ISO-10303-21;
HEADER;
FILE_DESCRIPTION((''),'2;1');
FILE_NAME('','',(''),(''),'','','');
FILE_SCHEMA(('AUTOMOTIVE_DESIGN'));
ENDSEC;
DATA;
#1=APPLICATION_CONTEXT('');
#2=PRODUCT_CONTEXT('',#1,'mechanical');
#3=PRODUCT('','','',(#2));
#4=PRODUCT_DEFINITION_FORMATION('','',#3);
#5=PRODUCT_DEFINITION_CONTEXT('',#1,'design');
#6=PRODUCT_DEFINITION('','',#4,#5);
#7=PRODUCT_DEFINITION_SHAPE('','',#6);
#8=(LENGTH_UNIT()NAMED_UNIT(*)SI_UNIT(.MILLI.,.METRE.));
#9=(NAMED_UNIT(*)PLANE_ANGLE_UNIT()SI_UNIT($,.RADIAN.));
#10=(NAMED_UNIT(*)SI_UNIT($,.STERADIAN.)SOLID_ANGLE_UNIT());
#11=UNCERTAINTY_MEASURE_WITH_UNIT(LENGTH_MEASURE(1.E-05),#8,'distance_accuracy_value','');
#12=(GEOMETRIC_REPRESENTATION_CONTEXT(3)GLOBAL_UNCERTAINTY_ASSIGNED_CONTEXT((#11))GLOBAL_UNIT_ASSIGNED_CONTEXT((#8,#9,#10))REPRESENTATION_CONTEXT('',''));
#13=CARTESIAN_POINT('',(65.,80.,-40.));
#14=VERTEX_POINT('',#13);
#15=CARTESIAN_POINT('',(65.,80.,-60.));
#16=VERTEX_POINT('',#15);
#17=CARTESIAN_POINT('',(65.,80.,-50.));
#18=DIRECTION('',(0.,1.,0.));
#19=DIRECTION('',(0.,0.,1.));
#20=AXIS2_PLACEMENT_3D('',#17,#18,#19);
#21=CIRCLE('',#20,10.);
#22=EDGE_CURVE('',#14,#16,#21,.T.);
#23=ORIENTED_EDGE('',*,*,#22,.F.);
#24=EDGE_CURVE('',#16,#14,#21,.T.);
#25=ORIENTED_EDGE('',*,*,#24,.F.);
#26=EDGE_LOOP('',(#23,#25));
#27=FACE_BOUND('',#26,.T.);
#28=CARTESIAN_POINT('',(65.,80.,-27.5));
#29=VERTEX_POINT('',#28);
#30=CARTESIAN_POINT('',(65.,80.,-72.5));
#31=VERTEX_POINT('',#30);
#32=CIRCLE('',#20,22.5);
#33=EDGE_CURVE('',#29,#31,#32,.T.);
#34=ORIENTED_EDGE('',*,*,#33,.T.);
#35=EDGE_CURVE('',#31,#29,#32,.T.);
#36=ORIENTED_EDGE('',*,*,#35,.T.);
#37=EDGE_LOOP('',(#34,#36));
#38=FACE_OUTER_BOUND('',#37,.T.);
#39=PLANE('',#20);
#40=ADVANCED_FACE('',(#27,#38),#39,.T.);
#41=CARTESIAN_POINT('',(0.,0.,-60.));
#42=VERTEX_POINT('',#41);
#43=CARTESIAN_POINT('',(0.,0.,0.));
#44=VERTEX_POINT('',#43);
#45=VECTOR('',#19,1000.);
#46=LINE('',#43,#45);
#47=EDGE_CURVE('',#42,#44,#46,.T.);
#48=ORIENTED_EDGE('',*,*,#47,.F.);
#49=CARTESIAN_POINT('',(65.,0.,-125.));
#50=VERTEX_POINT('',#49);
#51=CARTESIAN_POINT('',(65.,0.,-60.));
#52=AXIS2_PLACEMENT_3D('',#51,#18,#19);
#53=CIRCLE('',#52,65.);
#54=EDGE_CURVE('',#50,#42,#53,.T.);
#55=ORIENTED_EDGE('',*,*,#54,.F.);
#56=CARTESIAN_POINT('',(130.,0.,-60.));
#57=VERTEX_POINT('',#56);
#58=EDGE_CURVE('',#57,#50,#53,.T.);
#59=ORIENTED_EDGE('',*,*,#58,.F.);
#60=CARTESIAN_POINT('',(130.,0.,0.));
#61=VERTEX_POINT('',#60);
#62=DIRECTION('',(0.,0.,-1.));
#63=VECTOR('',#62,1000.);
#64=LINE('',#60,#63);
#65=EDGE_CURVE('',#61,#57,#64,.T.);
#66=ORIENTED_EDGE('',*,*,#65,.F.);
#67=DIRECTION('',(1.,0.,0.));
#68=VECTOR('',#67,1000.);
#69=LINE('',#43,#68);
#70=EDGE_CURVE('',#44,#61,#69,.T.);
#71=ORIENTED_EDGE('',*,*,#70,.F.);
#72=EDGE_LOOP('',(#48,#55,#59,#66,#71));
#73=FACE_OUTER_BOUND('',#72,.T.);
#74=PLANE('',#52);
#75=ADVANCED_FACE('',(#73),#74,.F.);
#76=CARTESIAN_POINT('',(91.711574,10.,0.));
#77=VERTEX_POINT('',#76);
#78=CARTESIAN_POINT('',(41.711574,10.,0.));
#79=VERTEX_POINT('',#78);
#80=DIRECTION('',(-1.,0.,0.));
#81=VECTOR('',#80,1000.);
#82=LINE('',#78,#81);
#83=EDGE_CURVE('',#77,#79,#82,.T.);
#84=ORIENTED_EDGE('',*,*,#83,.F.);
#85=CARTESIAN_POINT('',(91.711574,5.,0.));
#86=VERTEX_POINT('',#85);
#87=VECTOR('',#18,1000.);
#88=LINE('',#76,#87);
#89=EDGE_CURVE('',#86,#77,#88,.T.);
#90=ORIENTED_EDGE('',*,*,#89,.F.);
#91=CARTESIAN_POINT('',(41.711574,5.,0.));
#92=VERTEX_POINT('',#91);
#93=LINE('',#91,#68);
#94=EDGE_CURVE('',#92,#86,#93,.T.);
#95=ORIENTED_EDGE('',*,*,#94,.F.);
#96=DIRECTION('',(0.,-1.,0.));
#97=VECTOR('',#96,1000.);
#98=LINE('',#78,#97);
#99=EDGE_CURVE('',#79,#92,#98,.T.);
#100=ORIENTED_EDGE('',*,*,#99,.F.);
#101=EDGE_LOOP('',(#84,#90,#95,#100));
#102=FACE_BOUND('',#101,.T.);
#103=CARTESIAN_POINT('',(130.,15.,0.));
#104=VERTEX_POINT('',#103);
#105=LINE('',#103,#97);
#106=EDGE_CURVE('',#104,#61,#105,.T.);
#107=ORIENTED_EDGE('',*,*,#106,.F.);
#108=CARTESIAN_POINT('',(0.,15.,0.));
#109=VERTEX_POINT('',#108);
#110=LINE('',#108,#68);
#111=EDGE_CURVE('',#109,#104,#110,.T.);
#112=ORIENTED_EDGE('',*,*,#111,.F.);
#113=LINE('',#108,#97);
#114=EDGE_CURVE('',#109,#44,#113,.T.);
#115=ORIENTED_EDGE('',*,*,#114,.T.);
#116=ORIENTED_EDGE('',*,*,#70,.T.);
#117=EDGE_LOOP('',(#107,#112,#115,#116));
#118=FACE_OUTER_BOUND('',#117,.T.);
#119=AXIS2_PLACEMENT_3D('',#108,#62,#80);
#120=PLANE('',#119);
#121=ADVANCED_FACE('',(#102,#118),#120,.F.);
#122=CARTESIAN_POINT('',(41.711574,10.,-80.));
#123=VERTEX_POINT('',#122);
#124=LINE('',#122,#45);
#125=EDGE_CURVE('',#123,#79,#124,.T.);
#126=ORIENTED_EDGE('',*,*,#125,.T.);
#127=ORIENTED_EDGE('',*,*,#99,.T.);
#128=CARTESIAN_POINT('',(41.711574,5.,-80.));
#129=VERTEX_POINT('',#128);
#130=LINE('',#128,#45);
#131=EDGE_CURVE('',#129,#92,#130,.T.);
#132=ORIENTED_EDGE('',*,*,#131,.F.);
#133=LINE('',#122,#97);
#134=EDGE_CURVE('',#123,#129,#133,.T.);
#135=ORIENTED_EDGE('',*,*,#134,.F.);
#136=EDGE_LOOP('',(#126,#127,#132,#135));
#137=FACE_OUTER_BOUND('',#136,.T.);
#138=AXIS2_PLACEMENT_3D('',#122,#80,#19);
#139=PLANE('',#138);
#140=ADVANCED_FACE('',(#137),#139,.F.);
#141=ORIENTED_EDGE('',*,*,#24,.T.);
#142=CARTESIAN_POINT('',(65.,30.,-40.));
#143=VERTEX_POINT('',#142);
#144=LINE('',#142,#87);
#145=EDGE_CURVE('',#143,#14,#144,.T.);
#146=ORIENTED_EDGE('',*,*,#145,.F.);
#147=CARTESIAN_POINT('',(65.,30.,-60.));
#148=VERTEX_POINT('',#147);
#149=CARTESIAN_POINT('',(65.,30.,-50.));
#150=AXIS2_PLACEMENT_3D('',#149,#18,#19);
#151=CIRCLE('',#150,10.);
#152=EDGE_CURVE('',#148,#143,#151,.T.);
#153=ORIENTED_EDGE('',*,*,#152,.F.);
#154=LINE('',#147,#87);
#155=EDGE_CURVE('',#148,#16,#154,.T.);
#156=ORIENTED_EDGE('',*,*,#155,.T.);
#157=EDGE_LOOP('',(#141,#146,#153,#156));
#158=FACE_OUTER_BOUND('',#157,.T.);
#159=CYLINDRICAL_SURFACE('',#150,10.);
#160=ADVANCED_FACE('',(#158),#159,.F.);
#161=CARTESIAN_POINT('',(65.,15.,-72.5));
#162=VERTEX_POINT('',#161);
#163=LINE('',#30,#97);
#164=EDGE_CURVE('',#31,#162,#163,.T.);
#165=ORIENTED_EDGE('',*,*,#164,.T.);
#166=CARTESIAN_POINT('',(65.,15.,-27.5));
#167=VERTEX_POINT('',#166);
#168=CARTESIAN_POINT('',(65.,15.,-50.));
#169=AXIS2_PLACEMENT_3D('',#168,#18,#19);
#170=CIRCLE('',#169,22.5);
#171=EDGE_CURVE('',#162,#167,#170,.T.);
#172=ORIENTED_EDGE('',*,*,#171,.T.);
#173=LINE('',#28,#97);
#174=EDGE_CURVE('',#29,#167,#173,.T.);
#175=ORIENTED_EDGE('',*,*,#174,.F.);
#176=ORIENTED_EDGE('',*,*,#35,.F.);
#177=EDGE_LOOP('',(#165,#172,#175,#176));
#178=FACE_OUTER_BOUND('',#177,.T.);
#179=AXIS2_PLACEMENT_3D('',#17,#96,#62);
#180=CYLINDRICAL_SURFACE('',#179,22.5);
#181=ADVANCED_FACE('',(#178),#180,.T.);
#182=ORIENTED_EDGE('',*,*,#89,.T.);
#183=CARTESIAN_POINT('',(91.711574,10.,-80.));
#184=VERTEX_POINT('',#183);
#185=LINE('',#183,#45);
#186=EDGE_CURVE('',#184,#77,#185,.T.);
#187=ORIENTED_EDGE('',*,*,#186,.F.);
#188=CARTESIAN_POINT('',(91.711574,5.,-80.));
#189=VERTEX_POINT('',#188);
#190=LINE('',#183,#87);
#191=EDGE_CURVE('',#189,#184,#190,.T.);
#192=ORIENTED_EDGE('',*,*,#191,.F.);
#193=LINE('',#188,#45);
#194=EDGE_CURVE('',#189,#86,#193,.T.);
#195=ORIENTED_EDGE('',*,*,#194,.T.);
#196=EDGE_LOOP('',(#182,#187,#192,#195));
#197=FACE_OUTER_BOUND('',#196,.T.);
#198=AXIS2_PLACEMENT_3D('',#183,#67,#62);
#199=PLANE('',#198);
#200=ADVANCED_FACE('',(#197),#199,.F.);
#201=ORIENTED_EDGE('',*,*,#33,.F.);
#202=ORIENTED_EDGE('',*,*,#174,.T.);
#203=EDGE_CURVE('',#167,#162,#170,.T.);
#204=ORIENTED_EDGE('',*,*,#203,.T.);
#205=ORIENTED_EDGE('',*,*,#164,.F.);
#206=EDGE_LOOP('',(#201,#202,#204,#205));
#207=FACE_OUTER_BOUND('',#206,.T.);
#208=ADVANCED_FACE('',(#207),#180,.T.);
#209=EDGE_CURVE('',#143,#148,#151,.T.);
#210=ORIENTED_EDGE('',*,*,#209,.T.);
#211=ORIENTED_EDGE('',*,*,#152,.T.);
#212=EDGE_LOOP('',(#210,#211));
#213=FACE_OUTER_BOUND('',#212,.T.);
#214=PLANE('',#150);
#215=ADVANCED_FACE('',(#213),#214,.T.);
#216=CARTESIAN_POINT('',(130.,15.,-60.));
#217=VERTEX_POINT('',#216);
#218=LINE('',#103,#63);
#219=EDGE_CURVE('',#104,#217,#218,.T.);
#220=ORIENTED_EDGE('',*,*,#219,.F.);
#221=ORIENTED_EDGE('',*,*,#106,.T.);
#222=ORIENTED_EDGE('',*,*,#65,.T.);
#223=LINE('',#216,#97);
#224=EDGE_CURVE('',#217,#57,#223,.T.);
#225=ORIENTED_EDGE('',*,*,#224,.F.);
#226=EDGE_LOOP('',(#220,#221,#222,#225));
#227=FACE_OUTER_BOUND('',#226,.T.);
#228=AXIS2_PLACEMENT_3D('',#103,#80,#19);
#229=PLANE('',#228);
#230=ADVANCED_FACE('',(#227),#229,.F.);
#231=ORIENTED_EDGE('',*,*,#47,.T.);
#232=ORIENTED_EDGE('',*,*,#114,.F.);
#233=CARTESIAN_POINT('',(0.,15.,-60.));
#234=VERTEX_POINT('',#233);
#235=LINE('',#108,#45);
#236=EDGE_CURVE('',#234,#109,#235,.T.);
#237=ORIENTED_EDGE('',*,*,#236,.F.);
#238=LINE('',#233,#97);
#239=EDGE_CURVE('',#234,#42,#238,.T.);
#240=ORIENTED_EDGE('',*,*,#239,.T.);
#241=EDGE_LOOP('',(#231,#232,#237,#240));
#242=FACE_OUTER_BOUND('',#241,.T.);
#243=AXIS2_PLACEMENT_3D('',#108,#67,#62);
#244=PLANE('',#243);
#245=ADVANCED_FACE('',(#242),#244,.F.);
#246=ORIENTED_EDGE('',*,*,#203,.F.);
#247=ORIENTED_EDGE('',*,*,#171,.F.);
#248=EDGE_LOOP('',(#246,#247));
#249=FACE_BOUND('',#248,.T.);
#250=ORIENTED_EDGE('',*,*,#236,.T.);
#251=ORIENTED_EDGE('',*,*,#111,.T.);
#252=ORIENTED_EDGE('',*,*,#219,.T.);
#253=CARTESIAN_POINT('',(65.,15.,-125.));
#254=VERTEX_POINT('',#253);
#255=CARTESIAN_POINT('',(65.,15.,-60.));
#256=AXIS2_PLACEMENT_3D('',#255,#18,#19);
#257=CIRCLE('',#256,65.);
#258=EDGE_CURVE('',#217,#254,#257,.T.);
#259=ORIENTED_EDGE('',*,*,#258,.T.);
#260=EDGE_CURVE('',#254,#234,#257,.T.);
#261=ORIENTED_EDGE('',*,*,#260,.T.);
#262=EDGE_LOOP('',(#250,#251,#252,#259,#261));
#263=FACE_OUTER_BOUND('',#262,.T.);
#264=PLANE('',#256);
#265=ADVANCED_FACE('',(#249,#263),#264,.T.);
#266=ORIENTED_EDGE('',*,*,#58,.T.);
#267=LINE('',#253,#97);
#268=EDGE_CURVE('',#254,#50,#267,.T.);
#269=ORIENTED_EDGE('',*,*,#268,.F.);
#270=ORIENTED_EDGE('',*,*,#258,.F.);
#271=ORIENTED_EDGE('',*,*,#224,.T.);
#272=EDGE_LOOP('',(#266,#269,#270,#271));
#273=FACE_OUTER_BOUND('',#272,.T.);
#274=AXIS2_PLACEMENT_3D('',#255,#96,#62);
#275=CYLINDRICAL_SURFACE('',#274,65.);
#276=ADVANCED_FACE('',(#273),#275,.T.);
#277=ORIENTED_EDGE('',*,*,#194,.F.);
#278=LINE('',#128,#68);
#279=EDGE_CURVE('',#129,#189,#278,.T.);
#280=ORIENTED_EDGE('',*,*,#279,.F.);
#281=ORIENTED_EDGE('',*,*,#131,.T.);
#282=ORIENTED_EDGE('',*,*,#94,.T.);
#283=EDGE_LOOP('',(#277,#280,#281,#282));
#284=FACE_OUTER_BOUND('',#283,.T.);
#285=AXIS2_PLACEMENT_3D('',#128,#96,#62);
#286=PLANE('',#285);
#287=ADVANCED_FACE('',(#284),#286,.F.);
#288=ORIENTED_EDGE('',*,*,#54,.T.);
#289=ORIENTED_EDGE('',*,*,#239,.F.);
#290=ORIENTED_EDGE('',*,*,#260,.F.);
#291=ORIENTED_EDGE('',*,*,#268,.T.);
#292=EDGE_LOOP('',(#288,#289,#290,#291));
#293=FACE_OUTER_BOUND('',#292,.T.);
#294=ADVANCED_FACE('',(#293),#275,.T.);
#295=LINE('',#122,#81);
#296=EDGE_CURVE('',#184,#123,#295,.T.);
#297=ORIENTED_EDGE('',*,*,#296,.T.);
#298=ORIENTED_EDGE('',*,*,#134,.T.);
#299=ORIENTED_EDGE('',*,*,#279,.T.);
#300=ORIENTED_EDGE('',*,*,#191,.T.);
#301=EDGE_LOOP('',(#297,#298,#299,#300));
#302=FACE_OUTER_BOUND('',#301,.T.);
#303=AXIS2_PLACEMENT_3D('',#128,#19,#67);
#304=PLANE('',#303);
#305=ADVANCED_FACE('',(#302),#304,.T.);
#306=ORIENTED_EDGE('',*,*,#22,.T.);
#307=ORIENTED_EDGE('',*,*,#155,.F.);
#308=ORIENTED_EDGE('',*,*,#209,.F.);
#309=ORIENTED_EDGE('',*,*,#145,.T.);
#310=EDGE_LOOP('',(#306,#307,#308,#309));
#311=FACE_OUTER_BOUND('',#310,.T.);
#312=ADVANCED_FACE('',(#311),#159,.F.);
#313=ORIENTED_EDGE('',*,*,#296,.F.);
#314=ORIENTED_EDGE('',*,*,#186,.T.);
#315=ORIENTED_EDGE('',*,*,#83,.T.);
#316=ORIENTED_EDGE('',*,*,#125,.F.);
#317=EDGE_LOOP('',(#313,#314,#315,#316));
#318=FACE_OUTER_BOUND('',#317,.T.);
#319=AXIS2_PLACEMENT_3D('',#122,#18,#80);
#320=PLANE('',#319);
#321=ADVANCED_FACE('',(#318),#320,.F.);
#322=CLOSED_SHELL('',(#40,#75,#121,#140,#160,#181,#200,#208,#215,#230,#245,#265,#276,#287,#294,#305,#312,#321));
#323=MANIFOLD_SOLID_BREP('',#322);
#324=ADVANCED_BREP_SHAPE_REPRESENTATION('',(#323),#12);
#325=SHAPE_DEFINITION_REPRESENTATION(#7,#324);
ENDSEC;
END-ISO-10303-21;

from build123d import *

# Parameters (mm, degrees)
EXTRUDE_1_DEPTH     = 15
SKETCH_2_R          = 22.5
EXTRUDE_2_DEPTH     = 65
SKETCH_3_W          = 50
SKETCH_3_H          = 5
CUT_EXTRUDE_1_DEPTH = 80
SKETCH_4_R          = 10
CUT_EXTRUDE_2_DEPTH = 50


with BuildPart() as part:
    # 草图1 → 凸台-拉伸1 (new body)
    with BuildSketch(Plane(origin=(0, 0, 0), x_dir=(1, 0, 0), z_dir=(0, 1, 0))):
        with BuildLine():
            Line((0, 0), (130, 0))
            Line((130, 0), (130, 60))
            ThreePointArc((130, 60), (65, 125), (0, 60))
            Line((0, 60), (0, 0))
        make_face()
    extrude(amount=EXTRUDE_1_DEPTH)

    # 草图2 → 凸台-拉伸2 (add)
    with BuildSketch(Plane(origin=(0, 15, 0), x_dir=(1, 0, 0), z_dir=(0, 1, 0))):
        with Locations(Location((65, 50, 0), (0, 0, 270))):
            Circle(SKETCH_2_R)
    extrude(amount=EXTRUDE_2_DEPTH)

    # 草图3 → 切除-拉伸1 (cut)
    with BuildSketch(Plane.XY):
        with Locations((66.711573691, 7.5)):
            Rectangle(SKETCH_3_W, SKETCH_3_H)
    extrude(amount=-CUT_EXTRUDE_1_DEPTH, mode=Mode.SUBTRACT)

    # 草图4 → 切除-拉伸2 (cut)
    with BuildSketch(Plane(origin=(0, 80, 0), x_dir=(1, 0, 0), z_dir=(0, 1, 0))):
        with Locations(Location((65, 50, 0), (0, 0, 270))):
            Circle(SKETCH_4_R)
    extrude(amount=-CUT_EXTRUDE_2_DEPTH, mode=Mode.SUBTRACT)


solid = part.part
